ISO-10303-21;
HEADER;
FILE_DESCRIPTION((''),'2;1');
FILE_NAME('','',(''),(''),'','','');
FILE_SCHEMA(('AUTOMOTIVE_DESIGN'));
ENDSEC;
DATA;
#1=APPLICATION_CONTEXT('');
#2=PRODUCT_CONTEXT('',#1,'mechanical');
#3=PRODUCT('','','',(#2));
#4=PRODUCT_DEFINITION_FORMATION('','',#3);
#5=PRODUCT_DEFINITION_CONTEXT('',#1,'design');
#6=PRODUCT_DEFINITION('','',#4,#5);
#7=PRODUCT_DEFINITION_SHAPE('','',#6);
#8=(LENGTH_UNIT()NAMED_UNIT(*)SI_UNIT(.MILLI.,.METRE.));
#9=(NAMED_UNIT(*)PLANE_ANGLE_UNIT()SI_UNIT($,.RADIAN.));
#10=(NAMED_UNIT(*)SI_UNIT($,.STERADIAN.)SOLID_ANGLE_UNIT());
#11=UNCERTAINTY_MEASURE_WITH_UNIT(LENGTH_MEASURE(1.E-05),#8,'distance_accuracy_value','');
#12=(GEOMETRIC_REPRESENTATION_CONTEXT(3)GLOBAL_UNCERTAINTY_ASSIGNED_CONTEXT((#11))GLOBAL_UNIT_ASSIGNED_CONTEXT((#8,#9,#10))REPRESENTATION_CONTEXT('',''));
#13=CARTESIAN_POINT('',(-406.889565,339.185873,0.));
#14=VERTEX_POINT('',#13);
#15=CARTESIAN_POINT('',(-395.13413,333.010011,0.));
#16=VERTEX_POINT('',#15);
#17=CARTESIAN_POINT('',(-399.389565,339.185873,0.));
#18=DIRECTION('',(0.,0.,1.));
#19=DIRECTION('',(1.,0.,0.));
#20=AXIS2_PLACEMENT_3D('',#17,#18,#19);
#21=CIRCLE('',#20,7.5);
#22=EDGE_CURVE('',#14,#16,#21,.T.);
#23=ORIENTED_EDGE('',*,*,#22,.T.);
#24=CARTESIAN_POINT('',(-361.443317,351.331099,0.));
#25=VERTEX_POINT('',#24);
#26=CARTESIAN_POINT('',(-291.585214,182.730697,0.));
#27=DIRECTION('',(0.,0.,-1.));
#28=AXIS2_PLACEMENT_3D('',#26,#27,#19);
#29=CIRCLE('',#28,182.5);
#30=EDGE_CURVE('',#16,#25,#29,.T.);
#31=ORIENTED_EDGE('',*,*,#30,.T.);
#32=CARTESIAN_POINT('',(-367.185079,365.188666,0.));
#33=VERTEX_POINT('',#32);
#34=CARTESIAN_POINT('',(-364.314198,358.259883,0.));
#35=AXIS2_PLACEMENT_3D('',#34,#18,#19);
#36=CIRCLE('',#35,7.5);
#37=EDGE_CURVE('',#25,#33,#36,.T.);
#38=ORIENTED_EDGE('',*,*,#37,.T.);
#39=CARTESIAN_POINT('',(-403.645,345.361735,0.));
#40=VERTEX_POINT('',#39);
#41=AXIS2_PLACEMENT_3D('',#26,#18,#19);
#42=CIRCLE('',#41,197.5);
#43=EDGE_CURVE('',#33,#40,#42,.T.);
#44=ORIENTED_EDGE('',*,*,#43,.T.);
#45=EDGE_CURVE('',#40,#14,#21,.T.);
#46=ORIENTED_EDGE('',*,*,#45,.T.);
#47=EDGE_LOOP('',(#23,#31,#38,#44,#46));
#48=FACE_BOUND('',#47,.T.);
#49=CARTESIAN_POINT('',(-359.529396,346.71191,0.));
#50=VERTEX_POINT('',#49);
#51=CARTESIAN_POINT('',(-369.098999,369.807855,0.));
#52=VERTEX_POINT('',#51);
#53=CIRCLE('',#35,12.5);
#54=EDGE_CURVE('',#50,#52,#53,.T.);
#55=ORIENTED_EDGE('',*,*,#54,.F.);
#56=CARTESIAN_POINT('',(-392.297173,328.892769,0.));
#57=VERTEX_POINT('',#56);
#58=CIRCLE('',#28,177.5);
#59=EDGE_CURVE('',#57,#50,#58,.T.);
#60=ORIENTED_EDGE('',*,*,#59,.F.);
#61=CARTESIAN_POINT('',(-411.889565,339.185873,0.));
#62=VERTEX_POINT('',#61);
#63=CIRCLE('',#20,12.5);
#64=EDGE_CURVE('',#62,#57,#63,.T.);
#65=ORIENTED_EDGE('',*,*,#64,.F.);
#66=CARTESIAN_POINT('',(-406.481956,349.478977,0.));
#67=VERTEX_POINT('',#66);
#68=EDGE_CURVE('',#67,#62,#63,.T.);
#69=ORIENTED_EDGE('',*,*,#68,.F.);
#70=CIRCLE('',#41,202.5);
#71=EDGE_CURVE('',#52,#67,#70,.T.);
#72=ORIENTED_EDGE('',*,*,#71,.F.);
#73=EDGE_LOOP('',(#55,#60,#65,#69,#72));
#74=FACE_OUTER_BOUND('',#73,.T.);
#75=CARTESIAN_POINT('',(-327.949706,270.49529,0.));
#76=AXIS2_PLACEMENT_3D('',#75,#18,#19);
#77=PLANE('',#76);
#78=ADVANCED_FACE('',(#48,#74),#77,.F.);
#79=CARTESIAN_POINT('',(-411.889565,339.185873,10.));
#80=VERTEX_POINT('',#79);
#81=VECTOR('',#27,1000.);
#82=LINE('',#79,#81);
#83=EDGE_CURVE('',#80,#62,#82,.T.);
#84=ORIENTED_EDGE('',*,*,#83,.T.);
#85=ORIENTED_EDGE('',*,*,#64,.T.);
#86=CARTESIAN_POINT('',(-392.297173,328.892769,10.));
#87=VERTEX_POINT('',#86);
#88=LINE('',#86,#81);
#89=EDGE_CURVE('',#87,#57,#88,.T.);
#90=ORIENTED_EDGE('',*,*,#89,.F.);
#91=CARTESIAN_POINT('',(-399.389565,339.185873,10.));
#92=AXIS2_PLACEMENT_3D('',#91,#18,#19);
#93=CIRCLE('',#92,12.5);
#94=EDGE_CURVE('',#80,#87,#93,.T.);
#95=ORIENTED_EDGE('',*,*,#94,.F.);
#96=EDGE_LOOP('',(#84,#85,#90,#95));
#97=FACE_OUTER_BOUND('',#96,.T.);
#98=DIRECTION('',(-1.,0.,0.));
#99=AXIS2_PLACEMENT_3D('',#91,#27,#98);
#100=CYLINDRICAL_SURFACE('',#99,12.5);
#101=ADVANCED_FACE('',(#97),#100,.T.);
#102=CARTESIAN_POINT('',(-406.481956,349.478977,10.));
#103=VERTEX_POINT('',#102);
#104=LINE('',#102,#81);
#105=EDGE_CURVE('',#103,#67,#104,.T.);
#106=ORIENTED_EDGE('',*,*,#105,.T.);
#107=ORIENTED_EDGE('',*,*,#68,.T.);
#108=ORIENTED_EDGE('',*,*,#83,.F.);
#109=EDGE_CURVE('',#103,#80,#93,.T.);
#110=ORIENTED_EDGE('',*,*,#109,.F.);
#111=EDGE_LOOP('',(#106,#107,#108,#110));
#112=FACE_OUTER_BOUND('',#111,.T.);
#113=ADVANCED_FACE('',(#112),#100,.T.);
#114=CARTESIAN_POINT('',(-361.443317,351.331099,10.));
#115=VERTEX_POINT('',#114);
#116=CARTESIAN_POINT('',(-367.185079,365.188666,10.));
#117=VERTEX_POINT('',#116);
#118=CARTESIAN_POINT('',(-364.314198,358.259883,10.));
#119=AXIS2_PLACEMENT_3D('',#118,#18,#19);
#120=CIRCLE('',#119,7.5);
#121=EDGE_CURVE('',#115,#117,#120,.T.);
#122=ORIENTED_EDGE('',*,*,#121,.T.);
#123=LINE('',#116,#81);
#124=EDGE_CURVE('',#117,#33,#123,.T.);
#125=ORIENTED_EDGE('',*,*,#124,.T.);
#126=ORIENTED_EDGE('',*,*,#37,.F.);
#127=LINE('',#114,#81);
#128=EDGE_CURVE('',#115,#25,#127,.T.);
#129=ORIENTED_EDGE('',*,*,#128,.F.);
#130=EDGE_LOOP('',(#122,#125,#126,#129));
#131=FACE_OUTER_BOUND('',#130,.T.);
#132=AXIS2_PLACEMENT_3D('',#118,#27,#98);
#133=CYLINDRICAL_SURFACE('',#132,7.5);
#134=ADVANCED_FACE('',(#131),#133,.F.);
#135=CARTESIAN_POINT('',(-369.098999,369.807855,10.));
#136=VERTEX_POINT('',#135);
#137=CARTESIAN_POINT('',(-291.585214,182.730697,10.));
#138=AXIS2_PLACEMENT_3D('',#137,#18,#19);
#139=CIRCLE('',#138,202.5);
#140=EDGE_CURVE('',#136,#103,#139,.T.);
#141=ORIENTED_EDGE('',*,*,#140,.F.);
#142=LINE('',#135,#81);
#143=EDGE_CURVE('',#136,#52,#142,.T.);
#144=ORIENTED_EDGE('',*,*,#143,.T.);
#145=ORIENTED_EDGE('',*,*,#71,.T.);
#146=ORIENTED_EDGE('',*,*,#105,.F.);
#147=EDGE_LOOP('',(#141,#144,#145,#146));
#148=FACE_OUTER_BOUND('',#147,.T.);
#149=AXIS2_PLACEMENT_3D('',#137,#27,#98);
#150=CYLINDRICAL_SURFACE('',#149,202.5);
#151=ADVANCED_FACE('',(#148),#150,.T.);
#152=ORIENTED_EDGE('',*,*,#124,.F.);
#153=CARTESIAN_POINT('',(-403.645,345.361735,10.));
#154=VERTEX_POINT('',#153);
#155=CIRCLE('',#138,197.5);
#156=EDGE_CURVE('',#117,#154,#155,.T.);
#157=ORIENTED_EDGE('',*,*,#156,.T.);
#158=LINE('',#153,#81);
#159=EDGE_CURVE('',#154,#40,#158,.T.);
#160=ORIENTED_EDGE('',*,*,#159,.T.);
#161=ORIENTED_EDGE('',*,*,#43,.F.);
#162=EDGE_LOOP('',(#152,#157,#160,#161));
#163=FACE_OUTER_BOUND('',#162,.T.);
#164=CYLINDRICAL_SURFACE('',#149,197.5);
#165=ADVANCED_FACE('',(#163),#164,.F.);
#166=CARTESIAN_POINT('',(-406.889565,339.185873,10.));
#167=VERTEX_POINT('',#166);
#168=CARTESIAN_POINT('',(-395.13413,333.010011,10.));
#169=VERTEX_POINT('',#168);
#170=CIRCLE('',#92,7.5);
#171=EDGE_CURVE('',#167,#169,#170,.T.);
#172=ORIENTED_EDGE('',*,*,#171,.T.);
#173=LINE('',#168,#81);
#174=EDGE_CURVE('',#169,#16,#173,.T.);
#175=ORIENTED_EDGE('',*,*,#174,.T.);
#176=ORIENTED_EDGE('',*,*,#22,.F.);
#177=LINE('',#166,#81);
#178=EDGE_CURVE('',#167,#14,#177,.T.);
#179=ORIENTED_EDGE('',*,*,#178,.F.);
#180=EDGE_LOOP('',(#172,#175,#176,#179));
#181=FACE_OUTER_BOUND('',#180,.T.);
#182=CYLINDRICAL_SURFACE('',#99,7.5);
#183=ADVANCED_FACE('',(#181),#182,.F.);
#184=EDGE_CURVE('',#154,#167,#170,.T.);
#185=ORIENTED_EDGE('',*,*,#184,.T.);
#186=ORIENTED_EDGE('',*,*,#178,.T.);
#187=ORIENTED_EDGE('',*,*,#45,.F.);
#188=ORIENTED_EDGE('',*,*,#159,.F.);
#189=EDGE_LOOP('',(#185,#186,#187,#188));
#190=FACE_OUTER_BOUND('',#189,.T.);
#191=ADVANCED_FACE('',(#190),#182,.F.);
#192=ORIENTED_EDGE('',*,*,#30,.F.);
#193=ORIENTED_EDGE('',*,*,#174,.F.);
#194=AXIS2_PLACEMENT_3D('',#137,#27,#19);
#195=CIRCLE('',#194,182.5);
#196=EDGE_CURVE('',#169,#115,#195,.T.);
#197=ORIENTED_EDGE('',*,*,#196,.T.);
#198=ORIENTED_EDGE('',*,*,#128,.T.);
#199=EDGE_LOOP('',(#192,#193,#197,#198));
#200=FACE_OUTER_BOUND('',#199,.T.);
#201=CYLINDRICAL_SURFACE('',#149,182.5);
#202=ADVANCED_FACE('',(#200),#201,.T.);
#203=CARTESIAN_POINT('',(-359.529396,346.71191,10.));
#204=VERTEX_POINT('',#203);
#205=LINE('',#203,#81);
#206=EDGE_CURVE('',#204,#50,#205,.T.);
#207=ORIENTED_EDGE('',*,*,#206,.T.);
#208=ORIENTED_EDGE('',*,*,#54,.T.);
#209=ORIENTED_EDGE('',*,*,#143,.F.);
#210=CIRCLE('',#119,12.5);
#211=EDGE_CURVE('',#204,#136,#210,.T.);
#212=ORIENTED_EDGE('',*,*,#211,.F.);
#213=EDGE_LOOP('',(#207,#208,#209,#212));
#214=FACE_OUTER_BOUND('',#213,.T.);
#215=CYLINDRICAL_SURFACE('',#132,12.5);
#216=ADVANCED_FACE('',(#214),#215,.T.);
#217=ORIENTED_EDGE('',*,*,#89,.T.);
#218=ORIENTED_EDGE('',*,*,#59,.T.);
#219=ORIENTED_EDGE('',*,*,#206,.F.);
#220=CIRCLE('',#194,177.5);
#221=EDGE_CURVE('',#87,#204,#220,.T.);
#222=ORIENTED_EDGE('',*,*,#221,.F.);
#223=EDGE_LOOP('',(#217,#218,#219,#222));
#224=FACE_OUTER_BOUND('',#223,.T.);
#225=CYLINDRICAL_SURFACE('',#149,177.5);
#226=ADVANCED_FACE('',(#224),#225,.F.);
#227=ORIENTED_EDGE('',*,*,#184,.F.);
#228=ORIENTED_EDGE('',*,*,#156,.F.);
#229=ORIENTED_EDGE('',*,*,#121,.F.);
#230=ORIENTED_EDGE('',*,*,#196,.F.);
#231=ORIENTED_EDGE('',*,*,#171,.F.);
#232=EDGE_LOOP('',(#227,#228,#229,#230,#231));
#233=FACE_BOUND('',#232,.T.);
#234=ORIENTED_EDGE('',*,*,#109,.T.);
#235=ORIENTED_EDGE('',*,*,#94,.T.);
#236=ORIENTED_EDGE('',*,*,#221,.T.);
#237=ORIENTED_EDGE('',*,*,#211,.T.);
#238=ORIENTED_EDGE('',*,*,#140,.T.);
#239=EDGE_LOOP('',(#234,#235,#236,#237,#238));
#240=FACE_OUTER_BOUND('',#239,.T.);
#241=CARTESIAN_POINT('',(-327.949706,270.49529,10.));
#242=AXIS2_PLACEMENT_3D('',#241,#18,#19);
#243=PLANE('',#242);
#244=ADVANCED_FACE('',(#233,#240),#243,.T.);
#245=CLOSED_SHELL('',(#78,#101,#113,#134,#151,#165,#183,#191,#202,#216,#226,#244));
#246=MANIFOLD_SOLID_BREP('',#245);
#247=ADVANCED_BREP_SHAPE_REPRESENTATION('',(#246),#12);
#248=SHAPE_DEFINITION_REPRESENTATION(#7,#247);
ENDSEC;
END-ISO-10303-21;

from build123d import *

# Parameters (mm, degrees)
BOSS_EXTRUDE1_DEPTH = 10


with BuildPart() as part:
    # Sketch2 → Boss-Extrude1 (new body)
    with BuildSketch(Plane.XY):
        with BuildLine():
            ThreePointArc((-369.098999305, 369.807855403), (-388.32594275, 360.628087401), (-406.481956169, 349.478976603))
            ThreePointArc((-406.481956169, 349.478976603), (-409.682668352, 332.093481456), (-392.297173205, 328.892769272))
            ThreePointArc((-392.297173205, 328.892769272), (-376.382642925, 338.665446638), (-359.529396201, 346.711909949))
            ThreePointArc((-359.529396201, 346.711909949), (-352.766225026, 363.044684228), (-369.098999305, 369.807855403))
        make_face()
        with BuildLine():
            ThreePointArc((-367.185078684, 365.188666312), (-385.937282785, 356.235559249), (-403.644999576, 345.361735137))
            ThreePointArc((-403.644999576, 345.361735137), (-405.565426886, 334.930438049), (-395.134129798, 333.010010739))
            ThreePointArc((-395.134129798, 333.010010739), (-378.77130289, 343.057974791), (-361.443316822, 351.33109904))
            ThreePointArc((-361.443316822, 351.33109904), (-357.385414117, 361.130763607), (-367.185078684, 365.188666312))
        make_face(mode=Mode.SUBTRACT)
    extrude(amount=BOSS_EXTRUDE1_DEPTH)


solid = part.part
